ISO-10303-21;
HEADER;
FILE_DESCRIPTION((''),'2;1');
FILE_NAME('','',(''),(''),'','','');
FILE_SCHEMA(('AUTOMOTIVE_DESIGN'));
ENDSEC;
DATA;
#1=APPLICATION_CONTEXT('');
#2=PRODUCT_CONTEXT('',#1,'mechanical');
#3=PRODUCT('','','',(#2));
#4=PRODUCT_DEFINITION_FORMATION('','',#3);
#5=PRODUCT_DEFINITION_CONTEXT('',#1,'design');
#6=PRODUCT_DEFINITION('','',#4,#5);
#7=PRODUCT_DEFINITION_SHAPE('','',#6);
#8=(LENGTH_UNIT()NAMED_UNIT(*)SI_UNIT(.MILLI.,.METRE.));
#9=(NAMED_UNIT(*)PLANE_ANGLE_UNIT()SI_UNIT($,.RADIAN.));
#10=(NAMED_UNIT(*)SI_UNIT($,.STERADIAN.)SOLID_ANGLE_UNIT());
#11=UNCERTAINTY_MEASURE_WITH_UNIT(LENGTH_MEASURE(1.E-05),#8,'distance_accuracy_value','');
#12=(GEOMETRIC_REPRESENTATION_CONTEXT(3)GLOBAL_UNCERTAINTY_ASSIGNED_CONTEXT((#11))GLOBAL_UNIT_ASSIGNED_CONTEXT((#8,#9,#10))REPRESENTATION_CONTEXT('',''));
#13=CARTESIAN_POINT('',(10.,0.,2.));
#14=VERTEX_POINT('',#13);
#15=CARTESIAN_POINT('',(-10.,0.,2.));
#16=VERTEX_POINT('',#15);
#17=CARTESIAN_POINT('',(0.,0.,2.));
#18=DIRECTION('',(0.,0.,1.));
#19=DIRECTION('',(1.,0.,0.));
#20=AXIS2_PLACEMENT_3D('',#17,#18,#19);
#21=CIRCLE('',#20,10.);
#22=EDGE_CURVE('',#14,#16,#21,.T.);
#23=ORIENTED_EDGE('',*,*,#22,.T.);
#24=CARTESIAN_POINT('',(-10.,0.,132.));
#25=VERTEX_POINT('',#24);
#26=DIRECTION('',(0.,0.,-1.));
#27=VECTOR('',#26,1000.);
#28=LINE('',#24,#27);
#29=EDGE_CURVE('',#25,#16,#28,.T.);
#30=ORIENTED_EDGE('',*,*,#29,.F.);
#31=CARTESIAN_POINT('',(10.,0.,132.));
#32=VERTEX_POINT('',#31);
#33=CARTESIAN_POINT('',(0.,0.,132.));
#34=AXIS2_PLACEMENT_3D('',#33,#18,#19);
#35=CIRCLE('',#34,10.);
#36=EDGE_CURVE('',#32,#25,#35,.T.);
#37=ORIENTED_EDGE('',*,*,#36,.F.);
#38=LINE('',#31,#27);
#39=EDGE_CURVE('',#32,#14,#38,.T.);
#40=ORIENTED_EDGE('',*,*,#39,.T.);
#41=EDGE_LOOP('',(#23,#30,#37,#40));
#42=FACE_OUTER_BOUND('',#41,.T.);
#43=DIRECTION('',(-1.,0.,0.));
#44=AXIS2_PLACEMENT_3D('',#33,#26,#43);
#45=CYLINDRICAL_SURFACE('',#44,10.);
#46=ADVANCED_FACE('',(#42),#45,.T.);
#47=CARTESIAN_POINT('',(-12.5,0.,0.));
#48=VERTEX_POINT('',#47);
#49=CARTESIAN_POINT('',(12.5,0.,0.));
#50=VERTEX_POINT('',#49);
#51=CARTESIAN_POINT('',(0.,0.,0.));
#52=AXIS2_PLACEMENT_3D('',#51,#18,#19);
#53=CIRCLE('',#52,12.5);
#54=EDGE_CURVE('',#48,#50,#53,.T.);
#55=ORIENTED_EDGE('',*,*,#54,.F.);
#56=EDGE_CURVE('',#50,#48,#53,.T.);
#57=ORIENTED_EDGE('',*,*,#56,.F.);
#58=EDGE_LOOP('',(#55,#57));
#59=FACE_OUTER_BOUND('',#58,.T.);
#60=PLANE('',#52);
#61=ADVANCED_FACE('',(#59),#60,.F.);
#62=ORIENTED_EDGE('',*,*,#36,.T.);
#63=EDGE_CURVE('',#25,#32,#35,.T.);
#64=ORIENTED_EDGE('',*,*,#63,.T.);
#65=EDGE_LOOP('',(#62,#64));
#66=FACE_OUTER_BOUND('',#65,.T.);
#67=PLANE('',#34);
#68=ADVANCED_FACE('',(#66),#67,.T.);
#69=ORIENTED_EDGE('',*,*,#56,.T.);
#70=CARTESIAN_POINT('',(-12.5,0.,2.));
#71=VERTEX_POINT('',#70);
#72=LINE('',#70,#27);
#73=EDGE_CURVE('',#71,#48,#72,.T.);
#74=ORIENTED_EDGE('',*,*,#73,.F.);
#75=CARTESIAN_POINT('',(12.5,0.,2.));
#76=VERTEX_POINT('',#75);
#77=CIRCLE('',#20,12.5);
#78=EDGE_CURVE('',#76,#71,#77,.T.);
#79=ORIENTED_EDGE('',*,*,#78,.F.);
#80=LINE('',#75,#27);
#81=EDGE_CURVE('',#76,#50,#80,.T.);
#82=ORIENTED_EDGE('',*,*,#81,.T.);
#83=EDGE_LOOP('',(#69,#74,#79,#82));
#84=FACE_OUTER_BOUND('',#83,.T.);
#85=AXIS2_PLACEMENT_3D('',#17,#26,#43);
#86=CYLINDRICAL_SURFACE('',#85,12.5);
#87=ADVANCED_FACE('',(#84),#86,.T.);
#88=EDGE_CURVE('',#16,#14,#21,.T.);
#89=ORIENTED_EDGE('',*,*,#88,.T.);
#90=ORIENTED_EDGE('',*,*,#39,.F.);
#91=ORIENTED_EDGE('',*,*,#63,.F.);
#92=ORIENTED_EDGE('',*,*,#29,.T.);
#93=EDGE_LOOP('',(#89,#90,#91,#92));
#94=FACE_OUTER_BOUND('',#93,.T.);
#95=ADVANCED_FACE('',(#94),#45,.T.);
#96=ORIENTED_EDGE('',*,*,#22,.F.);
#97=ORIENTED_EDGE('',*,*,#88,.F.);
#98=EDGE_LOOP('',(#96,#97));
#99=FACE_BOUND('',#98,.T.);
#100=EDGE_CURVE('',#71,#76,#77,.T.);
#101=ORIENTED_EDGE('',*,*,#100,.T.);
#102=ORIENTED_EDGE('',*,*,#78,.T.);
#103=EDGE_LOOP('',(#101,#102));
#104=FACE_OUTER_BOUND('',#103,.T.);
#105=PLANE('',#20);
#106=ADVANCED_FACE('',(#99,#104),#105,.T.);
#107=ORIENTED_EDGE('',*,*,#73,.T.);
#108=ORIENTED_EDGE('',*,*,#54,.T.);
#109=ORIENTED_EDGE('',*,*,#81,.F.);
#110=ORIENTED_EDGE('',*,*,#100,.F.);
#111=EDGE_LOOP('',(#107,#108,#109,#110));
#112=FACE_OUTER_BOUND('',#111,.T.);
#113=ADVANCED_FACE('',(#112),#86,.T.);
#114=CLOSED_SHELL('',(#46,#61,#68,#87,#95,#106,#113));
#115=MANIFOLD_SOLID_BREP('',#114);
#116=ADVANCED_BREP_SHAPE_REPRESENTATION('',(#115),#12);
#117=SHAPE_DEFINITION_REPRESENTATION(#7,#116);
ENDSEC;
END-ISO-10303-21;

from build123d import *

# Parameters (mm, degrees)
SKETCH1_R           = 12.5
BOSS_EXTRUDE1_DEPTH = 2
SKETCH2_R           = 10
BOSS_EXTRUDE7_DEPTH = 130


with BuildPart() as part:
    # Sketch1 → Boss-Extrude1 (new body)
    with BuildSketch(Plane.XY):
        Circle(SKETCH1_R)
    extrude(amount=BOSS_EXTRUDE1_DEPTH)

    # Sketch2 → Boss-Extrude7 (add)
    with BuildSketch(Plane.XY.offset(2)):
        Circle(SKETCH2_R)
    extrude(amount=BOSS_EXTRUDE7_DEPTH)


solid = part.part
